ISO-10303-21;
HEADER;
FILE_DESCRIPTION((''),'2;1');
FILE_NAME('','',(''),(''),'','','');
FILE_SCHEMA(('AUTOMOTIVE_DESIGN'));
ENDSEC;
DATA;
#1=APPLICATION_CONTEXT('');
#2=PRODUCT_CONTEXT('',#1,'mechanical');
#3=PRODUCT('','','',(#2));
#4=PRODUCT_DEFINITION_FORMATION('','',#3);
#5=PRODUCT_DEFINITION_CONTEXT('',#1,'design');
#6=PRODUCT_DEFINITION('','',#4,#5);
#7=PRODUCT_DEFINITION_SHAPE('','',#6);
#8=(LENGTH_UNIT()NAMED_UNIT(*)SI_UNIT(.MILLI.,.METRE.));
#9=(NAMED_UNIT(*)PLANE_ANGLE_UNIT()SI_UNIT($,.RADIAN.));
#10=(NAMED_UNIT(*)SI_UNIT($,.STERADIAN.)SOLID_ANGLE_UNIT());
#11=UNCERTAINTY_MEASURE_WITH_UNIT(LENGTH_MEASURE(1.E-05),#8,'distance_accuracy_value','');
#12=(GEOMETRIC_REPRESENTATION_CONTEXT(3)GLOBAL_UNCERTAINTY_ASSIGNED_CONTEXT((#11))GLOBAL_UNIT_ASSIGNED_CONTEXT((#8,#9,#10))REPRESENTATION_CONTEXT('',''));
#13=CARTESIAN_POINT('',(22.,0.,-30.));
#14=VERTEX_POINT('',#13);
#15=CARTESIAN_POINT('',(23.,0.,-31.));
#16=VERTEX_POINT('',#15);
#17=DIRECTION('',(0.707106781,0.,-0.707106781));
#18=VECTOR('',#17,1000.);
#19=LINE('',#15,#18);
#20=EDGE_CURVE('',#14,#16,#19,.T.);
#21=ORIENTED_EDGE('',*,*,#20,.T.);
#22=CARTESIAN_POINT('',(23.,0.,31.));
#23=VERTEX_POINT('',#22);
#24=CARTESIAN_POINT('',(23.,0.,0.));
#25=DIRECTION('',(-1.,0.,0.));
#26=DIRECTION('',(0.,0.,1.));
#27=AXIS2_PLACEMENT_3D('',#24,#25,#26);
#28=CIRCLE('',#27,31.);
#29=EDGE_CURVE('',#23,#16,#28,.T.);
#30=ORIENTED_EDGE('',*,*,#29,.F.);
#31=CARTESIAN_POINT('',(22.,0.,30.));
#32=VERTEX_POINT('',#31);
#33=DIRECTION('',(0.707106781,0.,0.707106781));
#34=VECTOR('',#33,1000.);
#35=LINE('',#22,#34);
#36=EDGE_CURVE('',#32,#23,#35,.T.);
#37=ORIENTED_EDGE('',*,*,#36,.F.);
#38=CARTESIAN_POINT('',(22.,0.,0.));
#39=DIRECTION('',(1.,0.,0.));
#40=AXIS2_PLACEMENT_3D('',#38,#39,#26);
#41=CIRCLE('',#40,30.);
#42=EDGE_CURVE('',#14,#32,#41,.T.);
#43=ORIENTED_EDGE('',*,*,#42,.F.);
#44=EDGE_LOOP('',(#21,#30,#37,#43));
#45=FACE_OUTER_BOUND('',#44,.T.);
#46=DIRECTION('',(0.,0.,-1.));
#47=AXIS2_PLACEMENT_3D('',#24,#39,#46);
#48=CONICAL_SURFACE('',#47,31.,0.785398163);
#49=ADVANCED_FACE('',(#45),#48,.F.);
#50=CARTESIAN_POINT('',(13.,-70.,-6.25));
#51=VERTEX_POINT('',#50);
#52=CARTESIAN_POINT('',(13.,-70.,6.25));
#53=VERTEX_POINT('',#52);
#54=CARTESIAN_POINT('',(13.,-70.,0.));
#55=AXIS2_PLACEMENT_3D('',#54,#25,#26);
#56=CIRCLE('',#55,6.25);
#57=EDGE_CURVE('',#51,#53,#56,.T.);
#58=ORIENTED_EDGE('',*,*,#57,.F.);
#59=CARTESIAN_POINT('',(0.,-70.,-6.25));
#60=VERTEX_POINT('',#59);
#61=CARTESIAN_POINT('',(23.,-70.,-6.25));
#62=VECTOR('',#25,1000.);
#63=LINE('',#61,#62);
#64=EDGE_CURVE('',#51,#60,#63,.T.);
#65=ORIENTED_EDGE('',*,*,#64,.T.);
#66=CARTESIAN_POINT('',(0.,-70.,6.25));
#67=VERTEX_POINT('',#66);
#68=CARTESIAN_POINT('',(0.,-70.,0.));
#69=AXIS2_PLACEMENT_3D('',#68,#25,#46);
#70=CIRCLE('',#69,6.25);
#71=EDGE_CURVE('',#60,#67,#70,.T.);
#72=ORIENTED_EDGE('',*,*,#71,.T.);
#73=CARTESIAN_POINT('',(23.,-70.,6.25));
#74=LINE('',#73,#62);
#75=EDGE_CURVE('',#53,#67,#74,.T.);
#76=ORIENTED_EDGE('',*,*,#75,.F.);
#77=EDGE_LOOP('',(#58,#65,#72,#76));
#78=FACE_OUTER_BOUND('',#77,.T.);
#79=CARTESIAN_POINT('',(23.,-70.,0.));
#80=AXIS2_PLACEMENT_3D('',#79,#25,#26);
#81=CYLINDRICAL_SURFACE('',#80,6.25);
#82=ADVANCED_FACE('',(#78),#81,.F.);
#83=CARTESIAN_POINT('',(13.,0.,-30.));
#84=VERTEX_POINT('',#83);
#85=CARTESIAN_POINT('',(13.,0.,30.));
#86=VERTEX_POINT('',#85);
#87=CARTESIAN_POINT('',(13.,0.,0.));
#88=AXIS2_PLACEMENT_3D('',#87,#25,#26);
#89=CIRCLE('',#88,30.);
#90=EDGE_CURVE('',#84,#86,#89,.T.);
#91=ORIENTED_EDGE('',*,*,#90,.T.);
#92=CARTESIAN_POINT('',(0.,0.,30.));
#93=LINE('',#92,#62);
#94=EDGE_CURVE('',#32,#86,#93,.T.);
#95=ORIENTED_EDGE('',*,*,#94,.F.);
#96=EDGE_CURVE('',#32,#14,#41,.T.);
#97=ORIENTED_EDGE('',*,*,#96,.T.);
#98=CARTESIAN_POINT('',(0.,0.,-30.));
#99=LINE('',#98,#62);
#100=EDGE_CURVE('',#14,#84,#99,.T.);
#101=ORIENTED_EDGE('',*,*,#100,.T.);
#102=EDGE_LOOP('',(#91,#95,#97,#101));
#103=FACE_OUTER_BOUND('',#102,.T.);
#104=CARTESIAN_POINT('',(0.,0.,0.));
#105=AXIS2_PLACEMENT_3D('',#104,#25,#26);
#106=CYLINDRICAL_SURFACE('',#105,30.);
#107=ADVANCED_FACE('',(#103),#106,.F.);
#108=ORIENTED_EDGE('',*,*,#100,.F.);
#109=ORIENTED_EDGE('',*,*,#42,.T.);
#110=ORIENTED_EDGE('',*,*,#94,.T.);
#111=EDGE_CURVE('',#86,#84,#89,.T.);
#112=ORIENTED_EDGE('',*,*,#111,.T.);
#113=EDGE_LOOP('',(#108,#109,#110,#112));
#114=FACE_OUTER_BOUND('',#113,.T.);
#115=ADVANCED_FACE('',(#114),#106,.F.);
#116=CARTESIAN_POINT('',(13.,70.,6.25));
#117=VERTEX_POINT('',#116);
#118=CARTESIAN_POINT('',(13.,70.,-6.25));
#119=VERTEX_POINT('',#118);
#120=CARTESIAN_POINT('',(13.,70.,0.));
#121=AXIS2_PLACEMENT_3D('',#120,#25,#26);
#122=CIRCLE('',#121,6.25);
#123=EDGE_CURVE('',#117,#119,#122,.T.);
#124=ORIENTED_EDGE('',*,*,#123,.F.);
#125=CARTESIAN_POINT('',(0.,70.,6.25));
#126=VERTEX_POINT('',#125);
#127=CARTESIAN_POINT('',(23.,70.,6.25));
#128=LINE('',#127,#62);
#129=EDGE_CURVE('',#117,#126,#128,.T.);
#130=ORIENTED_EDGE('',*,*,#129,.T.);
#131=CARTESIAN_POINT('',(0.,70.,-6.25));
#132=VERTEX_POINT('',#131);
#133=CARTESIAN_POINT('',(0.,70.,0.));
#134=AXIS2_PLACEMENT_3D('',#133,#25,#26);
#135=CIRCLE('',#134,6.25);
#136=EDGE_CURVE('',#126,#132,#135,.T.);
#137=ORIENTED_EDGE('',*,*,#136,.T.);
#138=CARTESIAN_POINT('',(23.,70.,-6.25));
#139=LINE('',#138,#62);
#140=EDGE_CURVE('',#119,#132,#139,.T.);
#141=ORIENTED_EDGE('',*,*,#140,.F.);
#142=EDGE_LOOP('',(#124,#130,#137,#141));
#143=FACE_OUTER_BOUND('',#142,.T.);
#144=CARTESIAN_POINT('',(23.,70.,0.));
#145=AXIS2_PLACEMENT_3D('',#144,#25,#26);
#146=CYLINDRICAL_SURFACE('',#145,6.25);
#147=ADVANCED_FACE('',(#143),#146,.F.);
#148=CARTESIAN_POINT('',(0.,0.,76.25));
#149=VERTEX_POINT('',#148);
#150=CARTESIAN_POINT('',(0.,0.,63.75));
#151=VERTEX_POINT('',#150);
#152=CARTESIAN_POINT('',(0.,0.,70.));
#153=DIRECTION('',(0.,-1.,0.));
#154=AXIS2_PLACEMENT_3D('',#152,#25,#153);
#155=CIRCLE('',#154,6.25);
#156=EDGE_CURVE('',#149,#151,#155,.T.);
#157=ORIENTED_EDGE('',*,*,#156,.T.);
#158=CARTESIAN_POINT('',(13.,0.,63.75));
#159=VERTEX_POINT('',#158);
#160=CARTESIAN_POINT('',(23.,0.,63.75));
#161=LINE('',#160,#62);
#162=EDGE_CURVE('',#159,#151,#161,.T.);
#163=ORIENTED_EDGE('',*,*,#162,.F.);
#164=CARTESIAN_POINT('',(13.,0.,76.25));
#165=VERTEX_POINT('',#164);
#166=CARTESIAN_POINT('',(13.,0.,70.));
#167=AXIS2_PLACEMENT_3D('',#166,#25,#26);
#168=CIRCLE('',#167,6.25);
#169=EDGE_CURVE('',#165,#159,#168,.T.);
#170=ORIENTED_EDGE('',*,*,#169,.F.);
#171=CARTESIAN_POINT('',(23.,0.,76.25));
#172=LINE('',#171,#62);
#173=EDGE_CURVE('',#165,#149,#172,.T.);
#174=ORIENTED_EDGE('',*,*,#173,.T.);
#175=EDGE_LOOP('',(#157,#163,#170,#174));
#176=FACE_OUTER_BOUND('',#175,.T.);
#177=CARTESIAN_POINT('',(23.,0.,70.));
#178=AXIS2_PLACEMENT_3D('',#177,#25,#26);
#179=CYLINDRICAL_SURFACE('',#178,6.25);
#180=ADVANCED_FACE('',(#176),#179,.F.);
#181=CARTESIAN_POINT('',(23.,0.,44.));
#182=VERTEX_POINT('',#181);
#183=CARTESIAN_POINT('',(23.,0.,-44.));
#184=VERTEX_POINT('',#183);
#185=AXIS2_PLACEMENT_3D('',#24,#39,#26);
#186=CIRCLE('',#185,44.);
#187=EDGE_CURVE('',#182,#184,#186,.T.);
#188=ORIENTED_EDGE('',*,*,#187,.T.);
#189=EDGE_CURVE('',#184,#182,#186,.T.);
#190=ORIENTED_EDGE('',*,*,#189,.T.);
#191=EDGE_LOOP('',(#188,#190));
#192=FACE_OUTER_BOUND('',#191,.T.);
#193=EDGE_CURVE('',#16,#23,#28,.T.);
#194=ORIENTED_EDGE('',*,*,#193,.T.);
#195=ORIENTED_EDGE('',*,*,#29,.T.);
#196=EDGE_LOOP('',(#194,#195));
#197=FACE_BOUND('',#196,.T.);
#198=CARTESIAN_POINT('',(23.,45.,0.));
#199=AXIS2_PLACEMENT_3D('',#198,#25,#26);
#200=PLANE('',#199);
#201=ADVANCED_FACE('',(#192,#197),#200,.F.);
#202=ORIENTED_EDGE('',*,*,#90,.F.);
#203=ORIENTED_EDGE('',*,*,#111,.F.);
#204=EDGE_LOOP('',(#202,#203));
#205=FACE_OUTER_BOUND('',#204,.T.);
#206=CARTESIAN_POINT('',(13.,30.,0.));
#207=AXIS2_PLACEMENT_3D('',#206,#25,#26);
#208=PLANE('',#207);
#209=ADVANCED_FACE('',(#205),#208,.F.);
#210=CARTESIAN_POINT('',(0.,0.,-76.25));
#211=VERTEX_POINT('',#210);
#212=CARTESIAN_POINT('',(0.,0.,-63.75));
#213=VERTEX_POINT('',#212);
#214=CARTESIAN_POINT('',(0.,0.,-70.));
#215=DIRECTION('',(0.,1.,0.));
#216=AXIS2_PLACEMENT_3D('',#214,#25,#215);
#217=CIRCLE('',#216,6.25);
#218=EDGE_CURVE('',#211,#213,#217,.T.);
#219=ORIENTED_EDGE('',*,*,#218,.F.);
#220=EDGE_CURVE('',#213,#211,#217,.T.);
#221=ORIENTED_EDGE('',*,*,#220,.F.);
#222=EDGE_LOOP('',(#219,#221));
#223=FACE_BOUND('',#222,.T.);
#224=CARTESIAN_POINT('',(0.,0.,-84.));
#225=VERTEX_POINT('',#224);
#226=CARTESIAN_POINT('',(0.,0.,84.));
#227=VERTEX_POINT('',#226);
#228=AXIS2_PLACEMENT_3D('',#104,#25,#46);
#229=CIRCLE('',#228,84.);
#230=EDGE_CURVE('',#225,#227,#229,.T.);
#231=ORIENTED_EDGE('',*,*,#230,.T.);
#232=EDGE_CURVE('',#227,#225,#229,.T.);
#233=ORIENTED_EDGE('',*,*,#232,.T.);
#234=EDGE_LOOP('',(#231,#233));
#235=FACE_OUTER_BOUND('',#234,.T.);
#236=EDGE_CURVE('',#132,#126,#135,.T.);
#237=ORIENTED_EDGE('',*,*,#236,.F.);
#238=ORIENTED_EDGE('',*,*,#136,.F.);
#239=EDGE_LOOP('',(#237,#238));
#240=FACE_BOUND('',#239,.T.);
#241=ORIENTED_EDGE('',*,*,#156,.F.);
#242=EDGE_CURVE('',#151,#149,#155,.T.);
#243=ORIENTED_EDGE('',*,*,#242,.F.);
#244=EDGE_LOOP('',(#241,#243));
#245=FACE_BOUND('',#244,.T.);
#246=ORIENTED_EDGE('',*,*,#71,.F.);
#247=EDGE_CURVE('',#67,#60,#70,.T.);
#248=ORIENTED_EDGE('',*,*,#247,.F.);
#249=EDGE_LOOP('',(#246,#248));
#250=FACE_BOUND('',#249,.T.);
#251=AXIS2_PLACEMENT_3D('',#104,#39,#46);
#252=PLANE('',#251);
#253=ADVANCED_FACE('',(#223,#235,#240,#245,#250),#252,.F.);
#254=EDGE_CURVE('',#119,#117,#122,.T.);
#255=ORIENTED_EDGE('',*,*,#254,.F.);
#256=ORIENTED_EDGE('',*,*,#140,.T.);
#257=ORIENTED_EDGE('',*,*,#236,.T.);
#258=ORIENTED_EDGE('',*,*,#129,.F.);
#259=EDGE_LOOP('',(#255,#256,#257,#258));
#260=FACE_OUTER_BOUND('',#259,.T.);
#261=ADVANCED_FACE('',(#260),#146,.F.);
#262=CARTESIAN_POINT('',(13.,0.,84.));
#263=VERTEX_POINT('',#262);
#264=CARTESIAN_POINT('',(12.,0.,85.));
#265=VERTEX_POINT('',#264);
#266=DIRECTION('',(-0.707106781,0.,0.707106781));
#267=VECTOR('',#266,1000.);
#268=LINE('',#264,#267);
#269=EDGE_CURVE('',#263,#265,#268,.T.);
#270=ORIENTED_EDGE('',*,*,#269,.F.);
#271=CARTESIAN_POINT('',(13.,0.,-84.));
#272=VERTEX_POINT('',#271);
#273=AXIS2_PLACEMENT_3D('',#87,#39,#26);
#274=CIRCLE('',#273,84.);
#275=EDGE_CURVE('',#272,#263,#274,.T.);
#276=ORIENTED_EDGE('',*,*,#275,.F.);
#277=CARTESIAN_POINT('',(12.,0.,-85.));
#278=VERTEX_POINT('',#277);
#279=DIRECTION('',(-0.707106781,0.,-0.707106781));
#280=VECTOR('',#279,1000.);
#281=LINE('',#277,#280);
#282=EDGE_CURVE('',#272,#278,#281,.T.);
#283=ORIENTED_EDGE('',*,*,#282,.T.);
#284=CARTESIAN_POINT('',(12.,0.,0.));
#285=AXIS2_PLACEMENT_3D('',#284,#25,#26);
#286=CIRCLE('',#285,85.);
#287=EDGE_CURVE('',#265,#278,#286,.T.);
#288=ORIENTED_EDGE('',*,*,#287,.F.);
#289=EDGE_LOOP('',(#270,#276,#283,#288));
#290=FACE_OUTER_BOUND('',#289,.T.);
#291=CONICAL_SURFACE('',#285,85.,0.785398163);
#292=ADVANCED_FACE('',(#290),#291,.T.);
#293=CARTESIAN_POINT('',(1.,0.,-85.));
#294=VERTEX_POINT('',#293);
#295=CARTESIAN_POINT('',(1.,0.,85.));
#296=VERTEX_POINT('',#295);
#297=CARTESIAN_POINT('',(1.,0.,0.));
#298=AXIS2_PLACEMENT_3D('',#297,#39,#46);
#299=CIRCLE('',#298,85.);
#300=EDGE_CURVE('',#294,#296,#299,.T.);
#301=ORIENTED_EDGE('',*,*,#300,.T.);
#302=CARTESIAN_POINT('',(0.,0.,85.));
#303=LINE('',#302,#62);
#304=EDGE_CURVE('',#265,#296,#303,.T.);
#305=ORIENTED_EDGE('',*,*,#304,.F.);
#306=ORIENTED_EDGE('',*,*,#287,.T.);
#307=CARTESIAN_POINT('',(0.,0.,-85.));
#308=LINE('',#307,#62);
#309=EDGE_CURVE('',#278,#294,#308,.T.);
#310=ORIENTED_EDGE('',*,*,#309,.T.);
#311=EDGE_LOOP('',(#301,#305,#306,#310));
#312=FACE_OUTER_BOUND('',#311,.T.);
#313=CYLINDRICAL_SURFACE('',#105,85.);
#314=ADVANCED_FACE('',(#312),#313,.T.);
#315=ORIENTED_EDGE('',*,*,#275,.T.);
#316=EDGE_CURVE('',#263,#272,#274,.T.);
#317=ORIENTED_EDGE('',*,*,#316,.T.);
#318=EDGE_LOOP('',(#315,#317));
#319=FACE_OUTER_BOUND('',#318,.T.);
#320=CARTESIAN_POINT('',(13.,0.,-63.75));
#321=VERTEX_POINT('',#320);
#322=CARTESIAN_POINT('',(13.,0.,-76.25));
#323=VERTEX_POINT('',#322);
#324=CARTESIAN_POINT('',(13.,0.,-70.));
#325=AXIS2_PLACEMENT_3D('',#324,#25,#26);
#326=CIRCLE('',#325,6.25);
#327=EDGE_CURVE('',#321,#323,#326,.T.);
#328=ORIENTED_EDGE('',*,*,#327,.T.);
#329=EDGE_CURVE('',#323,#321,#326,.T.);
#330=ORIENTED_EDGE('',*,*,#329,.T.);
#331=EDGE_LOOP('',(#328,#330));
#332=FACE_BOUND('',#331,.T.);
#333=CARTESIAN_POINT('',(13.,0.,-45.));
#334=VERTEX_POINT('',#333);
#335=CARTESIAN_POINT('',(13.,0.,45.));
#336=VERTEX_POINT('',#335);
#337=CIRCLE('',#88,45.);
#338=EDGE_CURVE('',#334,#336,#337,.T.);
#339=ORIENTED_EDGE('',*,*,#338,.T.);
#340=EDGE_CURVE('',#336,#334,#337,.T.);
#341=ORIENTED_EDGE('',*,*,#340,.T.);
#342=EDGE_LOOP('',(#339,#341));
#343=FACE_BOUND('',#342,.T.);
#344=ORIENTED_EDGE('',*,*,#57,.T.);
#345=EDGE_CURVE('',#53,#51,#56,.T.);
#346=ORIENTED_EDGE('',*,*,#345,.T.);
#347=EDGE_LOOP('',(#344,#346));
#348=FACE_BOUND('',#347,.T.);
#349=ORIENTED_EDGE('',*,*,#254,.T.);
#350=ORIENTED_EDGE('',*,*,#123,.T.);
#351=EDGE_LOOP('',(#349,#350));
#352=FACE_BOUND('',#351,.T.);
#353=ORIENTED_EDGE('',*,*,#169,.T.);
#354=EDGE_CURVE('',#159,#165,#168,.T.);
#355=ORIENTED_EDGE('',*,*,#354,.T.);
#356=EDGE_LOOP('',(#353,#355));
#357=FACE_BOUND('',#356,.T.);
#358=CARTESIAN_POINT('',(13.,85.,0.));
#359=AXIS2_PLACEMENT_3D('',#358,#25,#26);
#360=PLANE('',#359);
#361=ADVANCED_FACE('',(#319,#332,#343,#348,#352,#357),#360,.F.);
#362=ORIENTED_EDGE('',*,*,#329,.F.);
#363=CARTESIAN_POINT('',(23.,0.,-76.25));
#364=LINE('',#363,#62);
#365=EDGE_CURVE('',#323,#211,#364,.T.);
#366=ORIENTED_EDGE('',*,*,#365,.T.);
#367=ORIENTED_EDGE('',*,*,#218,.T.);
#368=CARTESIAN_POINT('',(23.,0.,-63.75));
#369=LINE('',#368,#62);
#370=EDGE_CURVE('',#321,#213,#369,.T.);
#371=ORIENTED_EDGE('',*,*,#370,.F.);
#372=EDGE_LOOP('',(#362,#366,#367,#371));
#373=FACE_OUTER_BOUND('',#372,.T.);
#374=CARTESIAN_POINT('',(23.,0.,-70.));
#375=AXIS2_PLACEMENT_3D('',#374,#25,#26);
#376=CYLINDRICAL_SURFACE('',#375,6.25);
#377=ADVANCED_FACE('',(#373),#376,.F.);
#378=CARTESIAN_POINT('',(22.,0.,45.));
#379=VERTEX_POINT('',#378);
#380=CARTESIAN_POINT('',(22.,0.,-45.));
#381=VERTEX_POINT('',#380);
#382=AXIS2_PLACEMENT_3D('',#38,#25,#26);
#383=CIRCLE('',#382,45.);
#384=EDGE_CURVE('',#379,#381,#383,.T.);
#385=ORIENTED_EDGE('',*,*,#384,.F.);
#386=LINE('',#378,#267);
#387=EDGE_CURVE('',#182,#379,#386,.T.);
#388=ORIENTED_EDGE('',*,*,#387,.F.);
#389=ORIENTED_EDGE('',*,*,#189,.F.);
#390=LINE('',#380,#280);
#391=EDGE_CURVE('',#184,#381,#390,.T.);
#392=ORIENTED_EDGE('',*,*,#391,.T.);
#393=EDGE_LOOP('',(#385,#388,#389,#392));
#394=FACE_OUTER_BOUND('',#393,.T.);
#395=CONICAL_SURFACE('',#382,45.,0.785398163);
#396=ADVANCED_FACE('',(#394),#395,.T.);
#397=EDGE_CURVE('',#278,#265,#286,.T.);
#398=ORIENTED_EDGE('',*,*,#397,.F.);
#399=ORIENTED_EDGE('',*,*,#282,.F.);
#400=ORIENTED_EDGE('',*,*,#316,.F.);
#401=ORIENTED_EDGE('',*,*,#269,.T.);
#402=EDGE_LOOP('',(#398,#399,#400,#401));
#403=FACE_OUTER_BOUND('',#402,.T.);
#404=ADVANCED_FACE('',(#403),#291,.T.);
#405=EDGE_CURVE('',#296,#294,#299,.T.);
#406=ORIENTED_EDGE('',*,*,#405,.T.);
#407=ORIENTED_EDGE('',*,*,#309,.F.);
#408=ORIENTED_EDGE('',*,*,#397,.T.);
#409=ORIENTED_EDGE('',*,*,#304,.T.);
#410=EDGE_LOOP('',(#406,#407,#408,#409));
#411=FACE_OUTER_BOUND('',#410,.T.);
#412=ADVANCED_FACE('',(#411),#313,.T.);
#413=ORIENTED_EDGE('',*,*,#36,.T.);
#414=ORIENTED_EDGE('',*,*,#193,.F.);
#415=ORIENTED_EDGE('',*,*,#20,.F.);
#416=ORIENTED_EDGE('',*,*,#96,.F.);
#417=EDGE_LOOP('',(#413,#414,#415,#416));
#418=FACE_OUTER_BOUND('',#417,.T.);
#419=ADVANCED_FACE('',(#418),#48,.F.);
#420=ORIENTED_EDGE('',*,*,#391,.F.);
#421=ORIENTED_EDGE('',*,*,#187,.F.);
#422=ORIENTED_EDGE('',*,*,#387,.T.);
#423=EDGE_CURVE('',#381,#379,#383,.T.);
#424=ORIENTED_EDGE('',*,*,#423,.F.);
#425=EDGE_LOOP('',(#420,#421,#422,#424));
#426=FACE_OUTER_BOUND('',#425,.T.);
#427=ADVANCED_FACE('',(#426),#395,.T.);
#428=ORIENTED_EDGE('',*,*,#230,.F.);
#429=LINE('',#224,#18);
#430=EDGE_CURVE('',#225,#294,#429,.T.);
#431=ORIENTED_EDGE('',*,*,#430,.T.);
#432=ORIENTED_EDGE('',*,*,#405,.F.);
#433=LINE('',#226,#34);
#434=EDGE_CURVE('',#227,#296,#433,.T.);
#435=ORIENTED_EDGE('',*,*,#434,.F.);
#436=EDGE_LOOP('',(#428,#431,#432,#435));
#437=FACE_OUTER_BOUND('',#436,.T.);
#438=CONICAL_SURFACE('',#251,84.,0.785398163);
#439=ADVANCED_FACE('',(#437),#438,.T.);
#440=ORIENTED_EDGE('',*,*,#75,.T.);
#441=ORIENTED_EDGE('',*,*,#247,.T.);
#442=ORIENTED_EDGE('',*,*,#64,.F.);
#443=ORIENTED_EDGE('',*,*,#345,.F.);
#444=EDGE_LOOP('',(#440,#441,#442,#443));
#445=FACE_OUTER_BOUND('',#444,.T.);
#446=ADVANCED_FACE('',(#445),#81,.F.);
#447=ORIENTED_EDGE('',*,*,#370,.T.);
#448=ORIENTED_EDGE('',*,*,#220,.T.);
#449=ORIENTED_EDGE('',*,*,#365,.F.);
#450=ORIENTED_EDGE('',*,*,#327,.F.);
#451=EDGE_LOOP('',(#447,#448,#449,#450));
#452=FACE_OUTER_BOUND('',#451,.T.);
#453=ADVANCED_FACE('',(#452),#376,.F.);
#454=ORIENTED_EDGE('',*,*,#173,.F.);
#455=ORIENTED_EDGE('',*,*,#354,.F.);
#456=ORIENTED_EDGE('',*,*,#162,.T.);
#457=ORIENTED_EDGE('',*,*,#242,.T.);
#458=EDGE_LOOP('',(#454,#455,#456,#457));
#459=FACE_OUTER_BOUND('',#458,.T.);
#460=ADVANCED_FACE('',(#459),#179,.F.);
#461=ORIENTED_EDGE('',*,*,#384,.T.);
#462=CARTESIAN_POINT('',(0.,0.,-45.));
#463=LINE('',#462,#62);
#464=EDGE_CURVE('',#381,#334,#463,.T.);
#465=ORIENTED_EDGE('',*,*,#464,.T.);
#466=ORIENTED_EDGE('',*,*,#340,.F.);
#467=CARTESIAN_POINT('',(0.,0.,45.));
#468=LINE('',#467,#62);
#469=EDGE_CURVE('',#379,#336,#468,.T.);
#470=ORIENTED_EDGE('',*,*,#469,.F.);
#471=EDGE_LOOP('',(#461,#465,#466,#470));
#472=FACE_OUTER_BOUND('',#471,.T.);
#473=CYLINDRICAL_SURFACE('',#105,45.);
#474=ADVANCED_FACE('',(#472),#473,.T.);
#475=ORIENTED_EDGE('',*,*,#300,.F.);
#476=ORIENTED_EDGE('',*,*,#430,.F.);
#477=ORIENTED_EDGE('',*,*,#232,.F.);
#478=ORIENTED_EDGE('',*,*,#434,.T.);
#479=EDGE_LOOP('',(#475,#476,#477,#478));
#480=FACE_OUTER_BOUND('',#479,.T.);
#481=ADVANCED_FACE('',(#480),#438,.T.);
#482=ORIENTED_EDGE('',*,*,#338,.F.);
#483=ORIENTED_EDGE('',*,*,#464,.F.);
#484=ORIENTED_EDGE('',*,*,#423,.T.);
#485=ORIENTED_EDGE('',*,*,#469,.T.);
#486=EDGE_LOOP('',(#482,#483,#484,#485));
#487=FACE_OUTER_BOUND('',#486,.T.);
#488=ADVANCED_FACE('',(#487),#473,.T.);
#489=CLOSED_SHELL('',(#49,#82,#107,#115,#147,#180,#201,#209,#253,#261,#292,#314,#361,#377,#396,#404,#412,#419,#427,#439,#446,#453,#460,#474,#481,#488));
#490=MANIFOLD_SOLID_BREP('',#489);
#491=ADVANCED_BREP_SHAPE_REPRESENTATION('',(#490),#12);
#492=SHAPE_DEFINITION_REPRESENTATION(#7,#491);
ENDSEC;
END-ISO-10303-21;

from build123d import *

# Parameters (mm, degrees)
SKETCH_2_R               = 6.25
CUT_EXTRUDE_1_DEPTH      = 123.388724971
PATTERN_CIRCULAR_1_COUNT = 4
CHAMFER_1_SIZE           = 1


with BuildPart() as part:
    # 草图1 → 旋转1 (revolve)
    with BuildSketch(Plane.XY, mode=Mode.PRIVATE) as revolve_1_sk:
        Polygon((0, 0), (0, 85), (13, 85), (13, 45), (23, 45), (23, 30), (13, 30), (13, 0), align=None)
    revolve(revolve_1_sk.sketch.rotate(Axis((0, 0, 0), (1, 0, 0)), 90), axis=Axis((0, 0, 0), (1, 0, 0)))

    # 草图2 → 切除-拉伸1 (cut, through all)
    with BuildSketch(Plane.ZY):
        with Locations((0, 70)):
            Circle(SKETCH_2_R)
    cut_extrude_1 = extrude(amount=-CUT_EXTRUDE_1_DEPTH, mode=Mode.SUBTRACT)

    # 阵列(圆周)1: 切除-拉伸1 ×4 about axis
    pattern_circular_1_axis = Axis((0, 0, 0), (1, 0, 0))
    for i in range(1, PATTERN_CIRCULAR_1_COUNT):
        add(cut_extrude_1.rotate(pattern_circular_1_axis, i * 360 / PATTERN_CIRCULAR_1_COUNT), mode=Mode.SUBTRACT)

    # 倒角1
    chamfer_1_edges = [part.edges().sort_by_distance(p)[0] for p in [
        (23, 0, -30),
        (23, 0, -45),
        (13, 0, -85),
        (0, 0, -85),
    ]]
    chamfer(chamfer_1_edges, length=CHAMFER_1_SIZE)


solid = part.part
